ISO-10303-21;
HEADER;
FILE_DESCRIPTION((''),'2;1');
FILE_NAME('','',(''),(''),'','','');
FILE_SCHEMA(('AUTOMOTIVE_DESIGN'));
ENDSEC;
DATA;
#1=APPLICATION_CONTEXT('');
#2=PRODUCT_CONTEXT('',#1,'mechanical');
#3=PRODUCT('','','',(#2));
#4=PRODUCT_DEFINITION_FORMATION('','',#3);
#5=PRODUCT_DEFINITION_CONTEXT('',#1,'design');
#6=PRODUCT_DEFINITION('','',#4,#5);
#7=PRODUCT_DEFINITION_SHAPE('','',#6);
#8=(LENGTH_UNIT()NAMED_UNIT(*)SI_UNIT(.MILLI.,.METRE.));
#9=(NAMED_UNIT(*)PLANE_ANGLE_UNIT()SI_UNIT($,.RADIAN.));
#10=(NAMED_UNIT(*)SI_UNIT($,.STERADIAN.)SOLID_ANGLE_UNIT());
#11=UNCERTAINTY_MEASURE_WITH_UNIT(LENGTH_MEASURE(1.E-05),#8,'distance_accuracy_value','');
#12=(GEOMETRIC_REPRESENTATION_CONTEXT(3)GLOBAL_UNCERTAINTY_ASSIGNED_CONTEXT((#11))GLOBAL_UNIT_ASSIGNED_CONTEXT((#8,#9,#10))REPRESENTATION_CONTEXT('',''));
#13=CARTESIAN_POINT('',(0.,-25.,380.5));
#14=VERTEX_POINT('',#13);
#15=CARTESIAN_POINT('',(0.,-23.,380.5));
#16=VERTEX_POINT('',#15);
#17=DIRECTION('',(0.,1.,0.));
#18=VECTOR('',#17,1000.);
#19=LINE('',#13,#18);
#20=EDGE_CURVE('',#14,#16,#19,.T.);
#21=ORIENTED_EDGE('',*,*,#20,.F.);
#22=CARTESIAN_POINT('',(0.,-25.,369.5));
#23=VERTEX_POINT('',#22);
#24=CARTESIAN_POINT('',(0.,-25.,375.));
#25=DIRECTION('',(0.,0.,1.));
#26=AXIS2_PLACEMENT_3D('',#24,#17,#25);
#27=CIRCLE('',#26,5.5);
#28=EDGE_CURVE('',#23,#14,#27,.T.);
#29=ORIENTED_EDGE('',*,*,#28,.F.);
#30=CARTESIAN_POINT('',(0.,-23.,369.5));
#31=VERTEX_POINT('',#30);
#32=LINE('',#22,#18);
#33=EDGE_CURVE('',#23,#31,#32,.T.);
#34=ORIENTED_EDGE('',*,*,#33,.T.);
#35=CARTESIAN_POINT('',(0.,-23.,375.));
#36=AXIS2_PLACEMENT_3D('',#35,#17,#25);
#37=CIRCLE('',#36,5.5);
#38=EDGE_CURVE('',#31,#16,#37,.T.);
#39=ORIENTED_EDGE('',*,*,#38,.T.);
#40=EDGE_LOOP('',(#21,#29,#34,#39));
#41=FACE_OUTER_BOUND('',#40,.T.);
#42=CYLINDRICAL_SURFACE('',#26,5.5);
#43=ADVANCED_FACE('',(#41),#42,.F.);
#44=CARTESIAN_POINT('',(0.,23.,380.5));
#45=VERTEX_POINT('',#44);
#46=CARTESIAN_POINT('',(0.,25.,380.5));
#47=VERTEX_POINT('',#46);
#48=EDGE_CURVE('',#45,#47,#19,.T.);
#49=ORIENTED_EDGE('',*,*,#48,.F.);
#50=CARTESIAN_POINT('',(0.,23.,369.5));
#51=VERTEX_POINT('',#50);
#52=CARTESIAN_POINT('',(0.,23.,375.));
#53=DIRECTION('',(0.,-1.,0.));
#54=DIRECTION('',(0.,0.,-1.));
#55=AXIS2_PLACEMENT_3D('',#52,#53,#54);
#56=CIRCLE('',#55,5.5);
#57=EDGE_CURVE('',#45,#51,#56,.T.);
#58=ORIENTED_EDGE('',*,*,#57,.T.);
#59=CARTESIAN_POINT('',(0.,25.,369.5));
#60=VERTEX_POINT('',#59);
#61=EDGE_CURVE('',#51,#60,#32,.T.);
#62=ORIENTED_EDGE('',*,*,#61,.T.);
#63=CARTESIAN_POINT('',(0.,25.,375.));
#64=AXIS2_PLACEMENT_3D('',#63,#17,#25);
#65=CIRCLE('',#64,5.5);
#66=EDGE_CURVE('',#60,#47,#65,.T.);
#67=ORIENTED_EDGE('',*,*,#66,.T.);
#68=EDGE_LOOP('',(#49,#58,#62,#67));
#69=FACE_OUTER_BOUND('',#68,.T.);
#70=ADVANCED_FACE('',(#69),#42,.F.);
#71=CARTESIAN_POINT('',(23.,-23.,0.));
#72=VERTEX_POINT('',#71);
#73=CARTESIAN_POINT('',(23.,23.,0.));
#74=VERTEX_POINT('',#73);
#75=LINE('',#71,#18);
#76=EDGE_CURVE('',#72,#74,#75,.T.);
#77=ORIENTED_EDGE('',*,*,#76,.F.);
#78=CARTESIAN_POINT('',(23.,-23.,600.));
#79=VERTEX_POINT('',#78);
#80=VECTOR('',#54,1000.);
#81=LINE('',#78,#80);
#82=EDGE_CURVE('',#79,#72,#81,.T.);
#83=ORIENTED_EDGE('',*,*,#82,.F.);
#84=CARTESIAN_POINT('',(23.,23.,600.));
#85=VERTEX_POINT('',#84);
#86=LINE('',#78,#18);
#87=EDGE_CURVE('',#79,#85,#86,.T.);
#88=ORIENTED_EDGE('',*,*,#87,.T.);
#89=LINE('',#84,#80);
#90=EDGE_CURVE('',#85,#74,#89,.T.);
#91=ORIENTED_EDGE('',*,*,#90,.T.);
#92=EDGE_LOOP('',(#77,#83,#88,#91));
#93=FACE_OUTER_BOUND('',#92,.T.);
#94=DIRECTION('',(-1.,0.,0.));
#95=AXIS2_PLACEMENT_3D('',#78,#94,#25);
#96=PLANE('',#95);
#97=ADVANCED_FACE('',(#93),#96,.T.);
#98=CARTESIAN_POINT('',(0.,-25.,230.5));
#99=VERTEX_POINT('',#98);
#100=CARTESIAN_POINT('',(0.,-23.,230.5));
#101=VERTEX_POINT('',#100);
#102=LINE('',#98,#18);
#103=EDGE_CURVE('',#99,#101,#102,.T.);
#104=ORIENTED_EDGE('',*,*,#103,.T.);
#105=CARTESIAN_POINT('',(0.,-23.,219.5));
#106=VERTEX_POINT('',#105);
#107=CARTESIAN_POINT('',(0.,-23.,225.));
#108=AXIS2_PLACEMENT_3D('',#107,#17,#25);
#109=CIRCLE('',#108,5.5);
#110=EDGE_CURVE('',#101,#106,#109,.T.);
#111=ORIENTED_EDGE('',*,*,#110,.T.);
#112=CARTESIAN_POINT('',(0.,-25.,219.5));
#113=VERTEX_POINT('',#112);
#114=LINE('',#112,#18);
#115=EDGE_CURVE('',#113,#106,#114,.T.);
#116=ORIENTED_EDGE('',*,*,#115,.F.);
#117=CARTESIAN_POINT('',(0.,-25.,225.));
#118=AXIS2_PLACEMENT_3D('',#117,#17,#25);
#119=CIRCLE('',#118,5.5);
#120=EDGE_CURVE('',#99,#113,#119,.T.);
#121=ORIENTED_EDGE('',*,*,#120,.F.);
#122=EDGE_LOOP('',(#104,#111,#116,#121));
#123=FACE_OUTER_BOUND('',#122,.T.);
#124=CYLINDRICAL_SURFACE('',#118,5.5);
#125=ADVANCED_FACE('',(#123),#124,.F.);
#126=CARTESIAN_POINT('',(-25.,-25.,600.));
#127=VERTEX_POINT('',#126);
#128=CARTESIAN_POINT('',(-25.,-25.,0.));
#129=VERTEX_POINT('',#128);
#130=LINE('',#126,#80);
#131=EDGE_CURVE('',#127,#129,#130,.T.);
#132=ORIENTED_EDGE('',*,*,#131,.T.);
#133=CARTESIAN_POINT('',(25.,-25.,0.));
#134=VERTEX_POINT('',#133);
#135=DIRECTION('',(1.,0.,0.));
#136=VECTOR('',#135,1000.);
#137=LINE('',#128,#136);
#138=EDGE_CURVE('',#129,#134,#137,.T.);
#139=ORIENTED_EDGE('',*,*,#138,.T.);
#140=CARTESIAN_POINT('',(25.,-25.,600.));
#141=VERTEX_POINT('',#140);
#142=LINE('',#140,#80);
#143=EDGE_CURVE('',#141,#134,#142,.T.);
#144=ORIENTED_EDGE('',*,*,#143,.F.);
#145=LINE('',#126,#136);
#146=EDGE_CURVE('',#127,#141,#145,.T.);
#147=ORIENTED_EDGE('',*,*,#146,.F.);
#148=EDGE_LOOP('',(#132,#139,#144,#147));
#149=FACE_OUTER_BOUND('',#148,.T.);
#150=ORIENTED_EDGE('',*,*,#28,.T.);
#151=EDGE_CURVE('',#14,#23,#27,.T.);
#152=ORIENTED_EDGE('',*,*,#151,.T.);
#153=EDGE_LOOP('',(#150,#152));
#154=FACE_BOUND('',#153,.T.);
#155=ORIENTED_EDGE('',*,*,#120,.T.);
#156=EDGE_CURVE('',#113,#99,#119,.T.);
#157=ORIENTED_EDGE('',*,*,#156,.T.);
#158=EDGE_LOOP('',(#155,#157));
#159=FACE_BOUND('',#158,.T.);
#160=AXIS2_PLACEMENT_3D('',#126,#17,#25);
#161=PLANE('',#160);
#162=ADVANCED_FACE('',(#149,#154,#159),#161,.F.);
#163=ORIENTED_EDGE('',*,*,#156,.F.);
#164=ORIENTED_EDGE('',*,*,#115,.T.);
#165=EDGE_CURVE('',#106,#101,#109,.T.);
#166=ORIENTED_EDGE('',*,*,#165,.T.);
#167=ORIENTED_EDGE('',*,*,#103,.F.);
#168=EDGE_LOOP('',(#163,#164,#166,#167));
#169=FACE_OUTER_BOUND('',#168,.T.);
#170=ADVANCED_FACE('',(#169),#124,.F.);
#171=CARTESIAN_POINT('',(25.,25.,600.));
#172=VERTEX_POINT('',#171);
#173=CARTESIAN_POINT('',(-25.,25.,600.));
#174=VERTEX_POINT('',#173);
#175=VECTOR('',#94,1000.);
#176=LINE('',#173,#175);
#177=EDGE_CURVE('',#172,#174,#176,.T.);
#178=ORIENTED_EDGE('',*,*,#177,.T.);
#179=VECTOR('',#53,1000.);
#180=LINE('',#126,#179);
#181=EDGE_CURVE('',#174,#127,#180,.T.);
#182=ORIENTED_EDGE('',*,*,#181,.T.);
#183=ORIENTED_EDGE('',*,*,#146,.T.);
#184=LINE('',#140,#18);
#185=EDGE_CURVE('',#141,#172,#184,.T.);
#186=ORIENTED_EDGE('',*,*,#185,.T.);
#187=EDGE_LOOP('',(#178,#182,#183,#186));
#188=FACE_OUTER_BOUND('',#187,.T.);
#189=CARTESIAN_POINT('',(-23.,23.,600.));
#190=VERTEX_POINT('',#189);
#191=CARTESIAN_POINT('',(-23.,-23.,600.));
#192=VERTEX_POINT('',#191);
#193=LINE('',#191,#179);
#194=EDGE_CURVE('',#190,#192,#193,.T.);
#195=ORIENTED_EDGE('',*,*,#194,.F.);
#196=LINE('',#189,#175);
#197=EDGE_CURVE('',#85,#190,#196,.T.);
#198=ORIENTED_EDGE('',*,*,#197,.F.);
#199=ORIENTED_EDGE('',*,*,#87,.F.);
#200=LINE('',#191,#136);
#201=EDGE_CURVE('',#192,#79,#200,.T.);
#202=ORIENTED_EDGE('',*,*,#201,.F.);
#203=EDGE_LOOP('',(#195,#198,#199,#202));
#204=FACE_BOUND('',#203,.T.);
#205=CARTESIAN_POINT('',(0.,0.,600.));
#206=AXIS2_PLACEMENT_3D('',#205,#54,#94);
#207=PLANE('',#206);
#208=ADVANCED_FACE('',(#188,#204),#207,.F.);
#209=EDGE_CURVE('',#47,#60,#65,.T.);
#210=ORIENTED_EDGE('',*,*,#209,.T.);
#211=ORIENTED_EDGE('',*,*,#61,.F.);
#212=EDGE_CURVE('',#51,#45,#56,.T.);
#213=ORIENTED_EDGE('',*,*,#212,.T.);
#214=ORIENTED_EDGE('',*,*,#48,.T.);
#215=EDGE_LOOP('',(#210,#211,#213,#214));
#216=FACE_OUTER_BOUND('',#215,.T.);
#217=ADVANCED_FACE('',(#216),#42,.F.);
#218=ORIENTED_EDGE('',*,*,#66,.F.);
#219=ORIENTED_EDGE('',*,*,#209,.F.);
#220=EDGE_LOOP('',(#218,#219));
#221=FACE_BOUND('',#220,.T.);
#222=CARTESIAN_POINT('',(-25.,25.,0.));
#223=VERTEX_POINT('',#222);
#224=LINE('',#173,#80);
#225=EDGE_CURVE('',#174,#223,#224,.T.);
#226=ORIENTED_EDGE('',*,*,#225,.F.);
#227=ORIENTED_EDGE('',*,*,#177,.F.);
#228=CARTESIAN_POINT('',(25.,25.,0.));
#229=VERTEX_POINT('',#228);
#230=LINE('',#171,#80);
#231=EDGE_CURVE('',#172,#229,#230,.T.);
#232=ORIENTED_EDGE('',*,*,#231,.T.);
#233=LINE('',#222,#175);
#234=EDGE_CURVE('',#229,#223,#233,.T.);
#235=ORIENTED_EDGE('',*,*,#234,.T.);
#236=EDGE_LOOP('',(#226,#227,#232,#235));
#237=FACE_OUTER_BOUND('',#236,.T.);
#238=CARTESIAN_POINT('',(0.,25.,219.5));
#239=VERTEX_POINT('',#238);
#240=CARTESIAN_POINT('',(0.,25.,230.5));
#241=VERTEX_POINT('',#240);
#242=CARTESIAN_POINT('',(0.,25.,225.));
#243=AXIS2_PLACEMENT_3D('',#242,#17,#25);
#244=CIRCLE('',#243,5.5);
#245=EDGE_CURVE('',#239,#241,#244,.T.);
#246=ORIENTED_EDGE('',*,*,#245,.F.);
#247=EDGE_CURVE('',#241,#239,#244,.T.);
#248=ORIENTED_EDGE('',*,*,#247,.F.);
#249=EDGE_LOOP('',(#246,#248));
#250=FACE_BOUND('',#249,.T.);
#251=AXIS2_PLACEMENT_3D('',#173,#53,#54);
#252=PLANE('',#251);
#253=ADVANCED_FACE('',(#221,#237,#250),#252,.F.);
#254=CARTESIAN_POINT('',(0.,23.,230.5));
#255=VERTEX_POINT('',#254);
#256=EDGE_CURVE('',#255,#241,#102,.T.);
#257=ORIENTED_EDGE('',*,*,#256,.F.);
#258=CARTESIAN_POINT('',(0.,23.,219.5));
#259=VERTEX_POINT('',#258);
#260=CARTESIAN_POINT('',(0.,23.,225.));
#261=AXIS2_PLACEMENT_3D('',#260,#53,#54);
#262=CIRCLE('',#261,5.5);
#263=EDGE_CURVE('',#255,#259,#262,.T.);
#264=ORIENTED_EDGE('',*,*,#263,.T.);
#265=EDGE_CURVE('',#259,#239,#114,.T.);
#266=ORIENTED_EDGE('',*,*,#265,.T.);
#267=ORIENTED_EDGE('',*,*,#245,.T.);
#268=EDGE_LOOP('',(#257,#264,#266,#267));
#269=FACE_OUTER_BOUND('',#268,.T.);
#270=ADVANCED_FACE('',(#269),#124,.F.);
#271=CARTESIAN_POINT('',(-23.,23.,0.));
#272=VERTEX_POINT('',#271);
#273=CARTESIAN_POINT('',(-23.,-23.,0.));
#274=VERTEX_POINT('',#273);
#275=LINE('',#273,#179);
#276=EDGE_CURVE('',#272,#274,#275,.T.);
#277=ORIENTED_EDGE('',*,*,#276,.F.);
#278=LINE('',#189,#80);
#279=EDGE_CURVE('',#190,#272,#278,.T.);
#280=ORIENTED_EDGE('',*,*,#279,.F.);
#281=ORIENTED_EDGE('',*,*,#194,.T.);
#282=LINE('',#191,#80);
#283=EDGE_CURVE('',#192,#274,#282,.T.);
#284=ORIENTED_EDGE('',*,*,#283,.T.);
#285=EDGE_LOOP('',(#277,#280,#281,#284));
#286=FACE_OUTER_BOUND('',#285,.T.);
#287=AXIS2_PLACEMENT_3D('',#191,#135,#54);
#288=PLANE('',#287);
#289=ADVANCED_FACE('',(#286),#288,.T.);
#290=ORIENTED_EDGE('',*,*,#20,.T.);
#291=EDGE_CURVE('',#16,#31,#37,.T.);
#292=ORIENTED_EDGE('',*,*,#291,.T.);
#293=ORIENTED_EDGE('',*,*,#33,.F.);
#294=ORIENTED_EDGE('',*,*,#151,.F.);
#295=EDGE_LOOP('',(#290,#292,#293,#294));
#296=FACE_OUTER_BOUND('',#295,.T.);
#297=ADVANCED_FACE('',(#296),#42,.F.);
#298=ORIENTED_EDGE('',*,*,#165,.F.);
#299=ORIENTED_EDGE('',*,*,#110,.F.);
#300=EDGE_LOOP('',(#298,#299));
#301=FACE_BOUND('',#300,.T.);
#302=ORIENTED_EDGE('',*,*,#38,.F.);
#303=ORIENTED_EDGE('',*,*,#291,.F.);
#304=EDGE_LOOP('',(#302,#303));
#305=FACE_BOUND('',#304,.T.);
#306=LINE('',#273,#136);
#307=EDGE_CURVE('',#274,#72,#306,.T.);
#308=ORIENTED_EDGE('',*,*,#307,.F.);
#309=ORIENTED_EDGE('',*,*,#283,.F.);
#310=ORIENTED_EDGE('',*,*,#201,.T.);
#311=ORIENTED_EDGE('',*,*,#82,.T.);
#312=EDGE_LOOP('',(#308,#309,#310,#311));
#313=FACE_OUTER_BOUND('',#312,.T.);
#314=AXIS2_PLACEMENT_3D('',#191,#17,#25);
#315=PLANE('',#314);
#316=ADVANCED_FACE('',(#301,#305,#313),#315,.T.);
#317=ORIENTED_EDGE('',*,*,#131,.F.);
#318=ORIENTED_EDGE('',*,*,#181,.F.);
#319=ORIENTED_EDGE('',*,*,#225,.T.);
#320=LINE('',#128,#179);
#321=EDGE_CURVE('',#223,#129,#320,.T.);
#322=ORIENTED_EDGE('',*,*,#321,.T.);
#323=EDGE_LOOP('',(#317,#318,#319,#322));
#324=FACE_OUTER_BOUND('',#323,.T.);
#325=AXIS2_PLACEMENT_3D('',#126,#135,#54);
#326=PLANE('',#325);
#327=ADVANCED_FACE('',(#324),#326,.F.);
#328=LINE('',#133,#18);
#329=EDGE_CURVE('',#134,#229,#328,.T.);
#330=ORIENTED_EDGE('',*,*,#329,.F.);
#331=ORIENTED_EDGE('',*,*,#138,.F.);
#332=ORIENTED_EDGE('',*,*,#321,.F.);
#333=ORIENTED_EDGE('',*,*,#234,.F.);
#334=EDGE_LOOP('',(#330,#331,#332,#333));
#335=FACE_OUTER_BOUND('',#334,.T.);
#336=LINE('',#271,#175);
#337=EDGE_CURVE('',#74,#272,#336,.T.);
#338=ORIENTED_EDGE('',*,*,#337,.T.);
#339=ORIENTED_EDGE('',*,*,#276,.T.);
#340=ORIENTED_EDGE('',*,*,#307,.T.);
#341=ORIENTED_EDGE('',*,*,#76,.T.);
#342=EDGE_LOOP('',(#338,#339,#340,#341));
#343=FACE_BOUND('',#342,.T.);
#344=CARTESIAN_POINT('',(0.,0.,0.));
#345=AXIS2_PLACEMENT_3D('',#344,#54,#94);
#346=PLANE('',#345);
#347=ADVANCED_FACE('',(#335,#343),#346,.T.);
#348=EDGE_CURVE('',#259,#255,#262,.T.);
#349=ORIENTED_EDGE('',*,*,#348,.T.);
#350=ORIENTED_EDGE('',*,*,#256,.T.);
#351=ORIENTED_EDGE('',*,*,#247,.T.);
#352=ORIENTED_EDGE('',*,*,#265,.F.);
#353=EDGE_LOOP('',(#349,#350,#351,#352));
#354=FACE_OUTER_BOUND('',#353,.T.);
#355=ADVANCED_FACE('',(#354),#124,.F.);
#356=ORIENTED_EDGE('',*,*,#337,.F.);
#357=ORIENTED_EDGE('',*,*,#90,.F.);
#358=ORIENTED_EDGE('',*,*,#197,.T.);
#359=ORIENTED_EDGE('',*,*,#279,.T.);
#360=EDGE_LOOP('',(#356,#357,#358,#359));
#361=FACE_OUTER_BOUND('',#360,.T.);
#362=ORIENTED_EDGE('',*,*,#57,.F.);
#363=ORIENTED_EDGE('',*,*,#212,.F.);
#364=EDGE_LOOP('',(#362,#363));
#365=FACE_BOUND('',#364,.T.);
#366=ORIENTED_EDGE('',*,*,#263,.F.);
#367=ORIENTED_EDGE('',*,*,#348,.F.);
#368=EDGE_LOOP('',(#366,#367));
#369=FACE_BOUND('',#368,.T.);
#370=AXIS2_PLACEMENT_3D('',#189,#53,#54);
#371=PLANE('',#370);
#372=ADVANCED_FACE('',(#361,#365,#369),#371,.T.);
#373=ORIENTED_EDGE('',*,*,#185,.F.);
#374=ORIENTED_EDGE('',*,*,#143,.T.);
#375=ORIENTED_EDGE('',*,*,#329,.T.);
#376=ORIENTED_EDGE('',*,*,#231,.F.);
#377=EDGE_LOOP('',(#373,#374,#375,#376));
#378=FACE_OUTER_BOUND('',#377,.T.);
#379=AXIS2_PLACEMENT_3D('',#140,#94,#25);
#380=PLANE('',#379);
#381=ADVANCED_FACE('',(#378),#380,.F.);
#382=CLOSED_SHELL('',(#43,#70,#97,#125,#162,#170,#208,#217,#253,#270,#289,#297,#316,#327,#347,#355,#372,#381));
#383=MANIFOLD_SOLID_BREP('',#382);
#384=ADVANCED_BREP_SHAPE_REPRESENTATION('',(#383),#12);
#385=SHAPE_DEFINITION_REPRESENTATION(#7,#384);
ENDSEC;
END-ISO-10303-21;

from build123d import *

# Parameters (mm, degrees)
SKETCH1_W           = 50
SKETCH1_H           = 50
SKETCH1_W_2         = 46
SKETCH1_H_2         = 46
BOSS_EXTRUDE1_DEPTH = 600
SKETCH2_R           = 5.5
CUT_EXTRUDE1_DEPTH  = 50


with BuildPart() as part:
    # Sketch1 → Boss-Extrude1 (new body)
    with BuildSketch(Plane.XY):
        Rectangle(SKETCH1_W, SKETCH1_H)
        Rectangle(SKETCH1_W_2, SKETCH1_H_2, mode=Mode.SUBTRACT)
    extrude(amount=BOSS_EXTRUDE1_DEPTH)

    # Sketch2 → Cut-Extrude1 (cut)
    with BuildSketch(Plane(origin=(0, 25, 0), x_dir=(1, 0, 0), z_dir=(0, 1, 0))):
        with Locations(Location((0, -225, 0), (0, 0, 270))):
            Circle(SKETCH2_R)
        with Locations(Location((0, -375, 0), (0, 0, 270))):
            Circle(SKETCH2_R)
    extrude(amount=-CUT_EXTRUDE1_DEPTH, mode=Mode.SUBTRACT)


solid = part.part
